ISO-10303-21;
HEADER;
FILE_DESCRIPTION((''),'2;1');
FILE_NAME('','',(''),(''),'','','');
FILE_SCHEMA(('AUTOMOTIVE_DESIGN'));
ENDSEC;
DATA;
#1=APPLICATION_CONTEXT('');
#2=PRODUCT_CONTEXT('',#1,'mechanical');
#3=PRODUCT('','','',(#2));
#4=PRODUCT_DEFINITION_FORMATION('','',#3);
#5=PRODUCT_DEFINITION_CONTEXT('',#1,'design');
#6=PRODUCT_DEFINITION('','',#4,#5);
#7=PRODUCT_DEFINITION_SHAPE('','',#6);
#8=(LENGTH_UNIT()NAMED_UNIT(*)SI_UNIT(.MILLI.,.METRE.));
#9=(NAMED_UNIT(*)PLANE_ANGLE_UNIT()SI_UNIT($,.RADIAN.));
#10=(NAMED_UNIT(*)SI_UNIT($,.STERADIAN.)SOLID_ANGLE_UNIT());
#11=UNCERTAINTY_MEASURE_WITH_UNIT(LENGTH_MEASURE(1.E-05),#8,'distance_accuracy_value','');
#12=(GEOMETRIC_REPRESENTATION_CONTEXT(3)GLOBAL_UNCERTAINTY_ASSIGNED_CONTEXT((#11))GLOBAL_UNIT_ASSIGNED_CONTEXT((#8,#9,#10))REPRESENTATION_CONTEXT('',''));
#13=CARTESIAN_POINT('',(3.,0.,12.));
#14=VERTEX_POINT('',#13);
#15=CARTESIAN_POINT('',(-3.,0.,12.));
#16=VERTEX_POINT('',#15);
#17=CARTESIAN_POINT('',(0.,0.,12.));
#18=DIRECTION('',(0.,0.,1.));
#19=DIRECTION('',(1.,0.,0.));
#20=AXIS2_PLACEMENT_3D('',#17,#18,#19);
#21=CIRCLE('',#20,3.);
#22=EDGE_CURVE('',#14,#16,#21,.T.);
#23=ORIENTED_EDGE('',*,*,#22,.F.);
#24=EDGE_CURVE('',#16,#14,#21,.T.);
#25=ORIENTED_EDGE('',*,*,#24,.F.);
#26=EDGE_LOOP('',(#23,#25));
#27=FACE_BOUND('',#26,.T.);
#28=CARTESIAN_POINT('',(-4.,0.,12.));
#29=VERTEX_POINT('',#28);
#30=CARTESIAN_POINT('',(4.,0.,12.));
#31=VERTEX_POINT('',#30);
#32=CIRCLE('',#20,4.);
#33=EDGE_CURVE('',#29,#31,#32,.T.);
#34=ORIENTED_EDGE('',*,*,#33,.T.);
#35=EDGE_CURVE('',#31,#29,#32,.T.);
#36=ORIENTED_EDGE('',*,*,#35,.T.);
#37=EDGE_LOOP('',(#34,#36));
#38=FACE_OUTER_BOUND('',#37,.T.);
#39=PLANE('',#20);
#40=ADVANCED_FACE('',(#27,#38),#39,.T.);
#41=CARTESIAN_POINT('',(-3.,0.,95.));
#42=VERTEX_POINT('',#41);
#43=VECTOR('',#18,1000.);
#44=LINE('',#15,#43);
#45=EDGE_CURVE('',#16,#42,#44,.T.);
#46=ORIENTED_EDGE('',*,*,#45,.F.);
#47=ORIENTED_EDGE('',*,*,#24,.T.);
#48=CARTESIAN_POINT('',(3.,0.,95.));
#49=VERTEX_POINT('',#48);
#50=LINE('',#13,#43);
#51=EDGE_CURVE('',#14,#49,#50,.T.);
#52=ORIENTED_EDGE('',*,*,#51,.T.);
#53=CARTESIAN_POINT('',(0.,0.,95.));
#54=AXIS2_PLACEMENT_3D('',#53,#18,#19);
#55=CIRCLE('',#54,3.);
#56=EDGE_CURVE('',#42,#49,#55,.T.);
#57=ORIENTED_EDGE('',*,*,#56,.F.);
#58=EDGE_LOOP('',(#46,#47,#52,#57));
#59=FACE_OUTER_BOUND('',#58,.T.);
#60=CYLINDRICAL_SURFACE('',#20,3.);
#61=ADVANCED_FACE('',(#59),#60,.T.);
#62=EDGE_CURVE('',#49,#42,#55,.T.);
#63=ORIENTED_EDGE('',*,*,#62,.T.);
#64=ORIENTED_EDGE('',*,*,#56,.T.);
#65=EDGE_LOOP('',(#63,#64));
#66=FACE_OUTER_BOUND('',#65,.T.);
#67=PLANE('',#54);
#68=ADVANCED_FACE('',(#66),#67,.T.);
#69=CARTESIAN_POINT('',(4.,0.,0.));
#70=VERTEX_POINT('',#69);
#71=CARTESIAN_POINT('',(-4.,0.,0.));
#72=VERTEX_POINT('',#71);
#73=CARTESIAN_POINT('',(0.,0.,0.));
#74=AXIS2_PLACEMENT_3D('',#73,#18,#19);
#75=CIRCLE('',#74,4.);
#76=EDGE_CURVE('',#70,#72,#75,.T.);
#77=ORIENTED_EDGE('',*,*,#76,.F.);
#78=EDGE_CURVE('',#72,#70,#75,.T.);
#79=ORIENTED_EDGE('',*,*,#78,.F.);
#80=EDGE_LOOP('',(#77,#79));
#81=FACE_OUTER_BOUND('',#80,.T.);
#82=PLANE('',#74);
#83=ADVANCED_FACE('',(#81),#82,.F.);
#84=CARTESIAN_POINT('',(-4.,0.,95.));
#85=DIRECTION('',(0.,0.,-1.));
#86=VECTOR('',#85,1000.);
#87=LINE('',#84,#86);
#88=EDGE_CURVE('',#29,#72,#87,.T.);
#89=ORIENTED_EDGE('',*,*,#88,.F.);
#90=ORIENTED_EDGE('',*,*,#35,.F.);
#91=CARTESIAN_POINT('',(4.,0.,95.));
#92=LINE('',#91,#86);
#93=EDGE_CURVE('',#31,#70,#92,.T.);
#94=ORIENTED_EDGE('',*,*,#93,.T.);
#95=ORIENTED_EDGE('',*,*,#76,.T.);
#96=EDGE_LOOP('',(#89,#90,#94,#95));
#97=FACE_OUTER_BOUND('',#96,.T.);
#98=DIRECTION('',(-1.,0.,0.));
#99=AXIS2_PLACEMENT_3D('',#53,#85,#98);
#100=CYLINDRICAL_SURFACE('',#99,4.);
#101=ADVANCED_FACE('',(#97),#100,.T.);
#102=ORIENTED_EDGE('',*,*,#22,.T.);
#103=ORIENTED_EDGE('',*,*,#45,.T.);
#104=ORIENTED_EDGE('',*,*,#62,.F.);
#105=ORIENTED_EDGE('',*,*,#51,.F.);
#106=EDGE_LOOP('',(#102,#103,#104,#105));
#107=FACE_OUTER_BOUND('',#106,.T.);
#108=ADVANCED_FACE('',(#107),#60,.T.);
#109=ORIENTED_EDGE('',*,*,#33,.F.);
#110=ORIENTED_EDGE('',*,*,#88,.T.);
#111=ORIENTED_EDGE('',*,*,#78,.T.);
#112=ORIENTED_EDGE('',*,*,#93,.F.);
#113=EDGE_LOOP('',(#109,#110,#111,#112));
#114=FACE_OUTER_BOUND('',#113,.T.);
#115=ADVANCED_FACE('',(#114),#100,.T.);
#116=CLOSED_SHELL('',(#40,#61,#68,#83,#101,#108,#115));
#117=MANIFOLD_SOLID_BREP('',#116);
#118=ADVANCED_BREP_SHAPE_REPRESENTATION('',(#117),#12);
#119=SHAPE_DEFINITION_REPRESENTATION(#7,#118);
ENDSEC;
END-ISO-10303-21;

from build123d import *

# Parameters (mm, degrees)
SKETCH_1_R          = 4
EXTRUDE_1_DEPTH     = 95
CUT_EXTRUDE_START   = -83
SKETCH_2_R          = 4
SKETCH_2_R_2        = 3
CUT_EXTRUDE_1_DEPTH = 83


with BuildPart() as part:
    # 草图1 → 凸台-拉伸1 (new body)
    with BuildSketch(Plane.XY):
        Circle(SKETCH_1_R)
    extrude(amount=EXTRUDE_1_DEPTH)

    # 草图2 → 切除-拉伸1 (cut)
    with BuildSketch(Plane.XY.offset(95).offset(CUT_EXTRUDE_START)):
        Circle(SKETCH_2_R)
        Circle(SKETCH_2_R_2, mode=Mode.SUBTRACT)
    extrude(amount=CUT_EXTRUDE_1_DEPTH, mode=Mode.SUBTRACT)


solid = part.part
